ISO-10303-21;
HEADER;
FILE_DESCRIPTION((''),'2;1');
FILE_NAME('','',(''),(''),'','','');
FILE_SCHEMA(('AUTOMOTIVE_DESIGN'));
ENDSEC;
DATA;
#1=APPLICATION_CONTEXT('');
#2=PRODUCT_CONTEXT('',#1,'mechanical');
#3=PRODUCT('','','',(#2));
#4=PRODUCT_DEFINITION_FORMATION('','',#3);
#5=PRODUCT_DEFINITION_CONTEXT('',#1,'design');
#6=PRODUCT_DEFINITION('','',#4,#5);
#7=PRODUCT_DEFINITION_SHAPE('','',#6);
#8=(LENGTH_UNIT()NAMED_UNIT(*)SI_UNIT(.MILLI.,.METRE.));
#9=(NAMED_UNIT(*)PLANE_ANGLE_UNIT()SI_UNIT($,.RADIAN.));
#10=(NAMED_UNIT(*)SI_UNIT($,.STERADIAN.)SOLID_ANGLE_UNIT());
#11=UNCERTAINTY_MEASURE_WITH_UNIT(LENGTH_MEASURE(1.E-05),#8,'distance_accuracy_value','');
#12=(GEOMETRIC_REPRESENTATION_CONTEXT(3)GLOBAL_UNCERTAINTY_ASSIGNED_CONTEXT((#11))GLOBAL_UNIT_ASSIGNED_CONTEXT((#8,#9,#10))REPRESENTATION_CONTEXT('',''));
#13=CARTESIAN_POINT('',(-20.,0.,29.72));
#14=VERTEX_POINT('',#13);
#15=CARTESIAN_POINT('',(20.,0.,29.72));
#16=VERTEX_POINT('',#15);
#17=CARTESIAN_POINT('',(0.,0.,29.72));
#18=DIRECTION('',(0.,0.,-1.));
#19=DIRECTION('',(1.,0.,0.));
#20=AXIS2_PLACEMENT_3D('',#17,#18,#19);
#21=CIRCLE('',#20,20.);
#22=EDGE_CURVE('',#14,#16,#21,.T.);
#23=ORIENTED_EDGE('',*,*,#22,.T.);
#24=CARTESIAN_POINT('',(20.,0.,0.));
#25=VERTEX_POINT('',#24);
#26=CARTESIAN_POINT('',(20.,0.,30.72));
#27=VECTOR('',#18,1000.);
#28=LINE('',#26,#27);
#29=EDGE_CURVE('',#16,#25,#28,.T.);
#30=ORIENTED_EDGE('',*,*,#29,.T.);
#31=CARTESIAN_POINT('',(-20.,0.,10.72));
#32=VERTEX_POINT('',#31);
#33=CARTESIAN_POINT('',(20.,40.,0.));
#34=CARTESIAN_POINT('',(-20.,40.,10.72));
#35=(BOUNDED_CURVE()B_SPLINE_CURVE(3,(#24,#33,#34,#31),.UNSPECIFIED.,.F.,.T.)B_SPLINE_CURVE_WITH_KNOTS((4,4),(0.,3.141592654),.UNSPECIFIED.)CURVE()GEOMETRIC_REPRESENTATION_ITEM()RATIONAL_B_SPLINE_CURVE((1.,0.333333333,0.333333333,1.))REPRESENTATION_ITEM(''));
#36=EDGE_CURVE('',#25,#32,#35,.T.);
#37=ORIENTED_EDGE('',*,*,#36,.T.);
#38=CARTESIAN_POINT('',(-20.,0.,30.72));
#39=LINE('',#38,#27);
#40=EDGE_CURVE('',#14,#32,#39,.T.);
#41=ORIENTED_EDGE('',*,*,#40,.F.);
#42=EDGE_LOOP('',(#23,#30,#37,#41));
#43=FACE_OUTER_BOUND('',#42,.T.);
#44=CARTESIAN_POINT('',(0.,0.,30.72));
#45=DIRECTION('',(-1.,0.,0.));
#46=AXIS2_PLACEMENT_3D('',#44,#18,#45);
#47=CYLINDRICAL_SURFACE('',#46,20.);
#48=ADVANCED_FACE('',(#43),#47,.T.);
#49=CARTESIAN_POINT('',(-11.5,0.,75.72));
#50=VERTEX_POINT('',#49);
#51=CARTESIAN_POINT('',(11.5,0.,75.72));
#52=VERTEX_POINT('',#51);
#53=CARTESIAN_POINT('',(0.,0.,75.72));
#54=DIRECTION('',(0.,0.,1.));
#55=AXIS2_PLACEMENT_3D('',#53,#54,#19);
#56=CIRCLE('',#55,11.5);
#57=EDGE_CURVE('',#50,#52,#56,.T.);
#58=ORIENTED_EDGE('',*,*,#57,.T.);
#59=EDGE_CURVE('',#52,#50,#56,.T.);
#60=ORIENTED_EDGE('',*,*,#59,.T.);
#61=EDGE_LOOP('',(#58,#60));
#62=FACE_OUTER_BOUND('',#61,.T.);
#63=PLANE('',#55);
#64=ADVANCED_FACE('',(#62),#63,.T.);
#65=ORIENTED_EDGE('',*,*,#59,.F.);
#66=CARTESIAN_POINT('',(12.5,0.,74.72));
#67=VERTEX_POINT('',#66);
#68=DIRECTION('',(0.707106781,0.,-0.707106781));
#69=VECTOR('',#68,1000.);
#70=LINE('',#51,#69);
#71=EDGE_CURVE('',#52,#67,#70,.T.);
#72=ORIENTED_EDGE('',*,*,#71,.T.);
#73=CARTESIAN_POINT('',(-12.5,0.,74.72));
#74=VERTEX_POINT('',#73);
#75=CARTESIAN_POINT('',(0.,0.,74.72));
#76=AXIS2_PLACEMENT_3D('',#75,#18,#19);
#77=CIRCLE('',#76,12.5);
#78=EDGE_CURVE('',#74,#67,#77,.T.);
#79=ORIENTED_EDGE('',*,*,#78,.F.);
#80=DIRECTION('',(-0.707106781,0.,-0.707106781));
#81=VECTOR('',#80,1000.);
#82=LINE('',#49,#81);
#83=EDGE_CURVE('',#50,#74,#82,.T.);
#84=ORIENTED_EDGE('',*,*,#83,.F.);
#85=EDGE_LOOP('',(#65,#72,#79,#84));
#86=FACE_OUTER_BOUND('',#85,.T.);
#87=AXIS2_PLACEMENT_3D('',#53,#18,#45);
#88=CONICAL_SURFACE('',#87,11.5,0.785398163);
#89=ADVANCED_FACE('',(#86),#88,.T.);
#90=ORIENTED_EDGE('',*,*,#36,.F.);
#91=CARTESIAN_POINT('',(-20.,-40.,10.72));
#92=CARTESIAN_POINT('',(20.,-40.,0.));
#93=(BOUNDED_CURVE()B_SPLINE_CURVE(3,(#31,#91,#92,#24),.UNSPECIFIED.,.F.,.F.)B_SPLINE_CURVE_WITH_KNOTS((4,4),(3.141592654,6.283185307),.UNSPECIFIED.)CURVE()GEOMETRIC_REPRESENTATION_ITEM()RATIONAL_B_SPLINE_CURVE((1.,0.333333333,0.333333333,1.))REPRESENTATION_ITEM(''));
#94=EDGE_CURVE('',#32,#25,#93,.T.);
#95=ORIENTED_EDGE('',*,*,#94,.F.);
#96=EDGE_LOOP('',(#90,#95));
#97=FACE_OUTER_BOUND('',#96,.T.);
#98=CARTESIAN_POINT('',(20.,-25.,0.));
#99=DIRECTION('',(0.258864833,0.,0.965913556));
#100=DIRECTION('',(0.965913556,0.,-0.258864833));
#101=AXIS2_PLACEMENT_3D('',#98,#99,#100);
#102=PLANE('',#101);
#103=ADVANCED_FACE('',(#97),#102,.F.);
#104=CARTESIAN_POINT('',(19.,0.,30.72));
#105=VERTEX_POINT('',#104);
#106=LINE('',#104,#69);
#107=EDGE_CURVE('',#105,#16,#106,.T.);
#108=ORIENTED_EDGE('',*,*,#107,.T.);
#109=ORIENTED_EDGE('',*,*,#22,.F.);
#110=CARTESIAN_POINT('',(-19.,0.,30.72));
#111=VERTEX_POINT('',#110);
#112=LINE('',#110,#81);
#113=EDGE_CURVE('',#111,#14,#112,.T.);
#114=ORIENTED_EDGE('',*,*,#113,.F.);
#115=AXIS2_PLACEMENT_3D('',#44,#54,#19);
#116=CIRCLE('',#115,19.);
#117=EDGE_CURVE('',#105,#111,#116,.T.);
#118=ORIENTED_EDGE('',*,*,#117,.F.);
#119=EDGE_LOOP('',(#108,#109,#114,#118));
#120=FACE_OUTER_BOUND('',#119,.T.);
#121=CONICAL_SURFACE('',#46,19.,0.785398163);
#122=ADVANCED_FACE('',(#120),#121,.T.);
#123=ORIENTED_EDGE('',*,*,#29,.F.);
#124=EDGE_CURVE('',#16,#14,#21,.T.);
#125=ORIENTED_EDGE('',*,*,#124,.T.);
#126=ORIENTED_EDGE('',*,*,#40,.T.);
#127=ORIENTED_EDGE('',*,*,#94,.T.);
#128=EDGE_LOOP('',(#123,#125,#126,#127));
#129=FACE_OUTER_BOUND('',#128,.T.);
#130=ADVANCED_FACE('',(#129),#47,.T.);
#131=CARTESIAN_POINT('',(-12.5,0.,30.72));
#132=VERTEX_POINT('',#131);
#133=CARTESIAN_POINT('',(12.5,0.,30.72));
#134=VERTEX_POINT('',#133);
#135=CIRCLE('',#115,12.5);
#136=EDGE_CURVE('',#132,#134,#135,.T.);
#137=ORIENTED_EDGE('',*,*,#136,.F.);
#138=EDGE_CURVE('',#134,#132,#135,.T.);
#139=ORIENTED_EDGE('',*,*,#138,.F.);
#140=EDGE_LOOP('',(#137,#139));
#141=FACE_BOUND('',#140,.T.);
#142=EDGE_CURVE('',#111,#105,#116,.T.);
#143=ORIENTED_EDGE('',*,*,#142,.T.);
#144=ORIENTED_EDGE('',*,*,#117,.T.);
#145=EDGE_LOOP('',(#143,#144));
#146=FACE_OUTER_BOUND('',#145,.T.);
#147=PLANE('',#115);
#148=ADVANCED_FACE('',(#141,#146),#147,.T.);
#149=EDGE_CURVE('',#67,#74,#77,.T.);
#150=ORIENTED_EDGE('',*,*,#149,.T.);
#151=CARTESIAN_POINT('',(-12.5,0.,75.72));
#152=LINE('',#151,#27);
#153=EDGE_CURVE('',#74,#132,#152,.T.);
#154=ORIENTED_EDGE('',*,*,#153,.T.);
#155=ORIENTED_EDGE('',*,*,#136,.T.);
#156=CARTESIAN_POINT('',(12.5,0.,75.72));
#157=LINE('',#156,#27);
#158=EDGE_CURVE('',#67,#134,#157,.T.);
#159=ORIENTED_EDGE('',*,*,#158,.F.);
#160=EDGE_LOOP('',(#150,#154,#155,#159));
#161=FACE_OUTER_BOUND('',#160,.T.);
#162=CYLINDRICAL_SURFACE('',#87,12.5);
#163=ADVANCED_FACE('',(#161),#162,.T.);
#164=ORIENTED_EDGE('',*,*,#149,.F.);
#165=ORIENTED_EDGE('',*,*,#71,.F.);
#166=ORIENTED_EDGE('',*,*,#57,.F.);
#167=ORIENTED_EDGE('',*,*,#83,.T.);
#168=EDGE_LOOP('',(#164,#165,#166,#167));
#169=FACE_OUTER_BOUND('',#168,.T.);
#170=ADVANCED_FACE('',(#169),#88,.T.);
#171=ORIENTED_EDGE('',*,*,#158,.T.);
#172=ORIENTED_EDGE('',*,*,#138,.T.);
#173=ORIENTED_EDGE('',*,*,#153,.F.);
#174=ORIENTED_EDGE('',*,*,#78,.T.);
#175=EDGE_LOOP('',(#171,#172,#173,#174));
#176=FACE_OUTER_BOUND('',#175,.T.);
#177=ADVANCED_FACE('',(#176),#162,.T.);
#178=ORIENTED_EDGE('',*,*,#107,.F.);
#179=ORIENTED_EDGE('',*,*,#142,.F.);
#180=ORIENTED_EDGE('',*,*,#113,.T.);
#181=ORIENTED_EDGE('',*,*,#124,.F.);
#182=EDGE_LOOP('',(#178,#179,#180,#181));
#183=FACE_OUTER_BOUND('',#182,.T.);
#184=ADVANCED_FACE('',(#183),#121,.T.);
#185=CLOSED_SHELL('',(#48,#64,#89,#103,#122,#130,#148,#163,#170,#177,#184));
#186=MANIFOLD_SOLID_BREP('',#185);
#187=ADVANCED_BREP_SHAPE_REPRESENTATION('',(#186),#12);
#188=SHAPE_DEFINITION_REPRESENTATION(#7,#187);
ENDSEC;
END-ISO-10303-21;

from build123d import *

# Parameters (mm, degrees)
SKETCH_1_R          = 20
EXTRUDE_1_DEPTH     = 30.72
SKETCH_2_R          = 12.5
EXTRUDE_2_DEPTH     = 45
CUT_EXTRUDE_1_DEPTH = 25
CHAMFER_1_SIZE      = 1


with BuildPart() as part:
    # 草图1 → 凸台-拉伸1 (new body)
    with BuildSketch(Plane.XY):
        Circle(SKETCH_1_R)
    extrude(amount=EXTRUDE_1_DEPTH)

    # 草图2 → 凸台-拉伸2 (add)
    with BuildSketch(Plane.XY.offset(30.72)):
        with Locations(Location((0, 0, 0), (0, 0, 180))):
            Circle(SKETCH_2_R)
    extrude(amount=EXTRUDE_2_DEPTH)

    # 草图3 → 切除-拉伸1 (cut, symmetric)
    with BuildSketch(Plane(origin=(0, 0, 0), x_dir=(1, 0, 0), z_dir=(0, 1, 0))):
        Polygon((-20, 0), (20, 0), (-20, -10.72), align=None)
    extrude(amount=CUT_EXTRUDE_1_DEPTH, both=True, mode=Mode.SUBTRACT)

    # 倒角1
    chamfer_1_edges = [part.edges().sort_by_distance(p)[0] for p in [
        (-20, 0, 30.72),
        (12.5, 0, 75.72),
    ]]
    chamfer(chamfer_1_edges, length=CHAMFER_1_SIZE)


solid = part.part
